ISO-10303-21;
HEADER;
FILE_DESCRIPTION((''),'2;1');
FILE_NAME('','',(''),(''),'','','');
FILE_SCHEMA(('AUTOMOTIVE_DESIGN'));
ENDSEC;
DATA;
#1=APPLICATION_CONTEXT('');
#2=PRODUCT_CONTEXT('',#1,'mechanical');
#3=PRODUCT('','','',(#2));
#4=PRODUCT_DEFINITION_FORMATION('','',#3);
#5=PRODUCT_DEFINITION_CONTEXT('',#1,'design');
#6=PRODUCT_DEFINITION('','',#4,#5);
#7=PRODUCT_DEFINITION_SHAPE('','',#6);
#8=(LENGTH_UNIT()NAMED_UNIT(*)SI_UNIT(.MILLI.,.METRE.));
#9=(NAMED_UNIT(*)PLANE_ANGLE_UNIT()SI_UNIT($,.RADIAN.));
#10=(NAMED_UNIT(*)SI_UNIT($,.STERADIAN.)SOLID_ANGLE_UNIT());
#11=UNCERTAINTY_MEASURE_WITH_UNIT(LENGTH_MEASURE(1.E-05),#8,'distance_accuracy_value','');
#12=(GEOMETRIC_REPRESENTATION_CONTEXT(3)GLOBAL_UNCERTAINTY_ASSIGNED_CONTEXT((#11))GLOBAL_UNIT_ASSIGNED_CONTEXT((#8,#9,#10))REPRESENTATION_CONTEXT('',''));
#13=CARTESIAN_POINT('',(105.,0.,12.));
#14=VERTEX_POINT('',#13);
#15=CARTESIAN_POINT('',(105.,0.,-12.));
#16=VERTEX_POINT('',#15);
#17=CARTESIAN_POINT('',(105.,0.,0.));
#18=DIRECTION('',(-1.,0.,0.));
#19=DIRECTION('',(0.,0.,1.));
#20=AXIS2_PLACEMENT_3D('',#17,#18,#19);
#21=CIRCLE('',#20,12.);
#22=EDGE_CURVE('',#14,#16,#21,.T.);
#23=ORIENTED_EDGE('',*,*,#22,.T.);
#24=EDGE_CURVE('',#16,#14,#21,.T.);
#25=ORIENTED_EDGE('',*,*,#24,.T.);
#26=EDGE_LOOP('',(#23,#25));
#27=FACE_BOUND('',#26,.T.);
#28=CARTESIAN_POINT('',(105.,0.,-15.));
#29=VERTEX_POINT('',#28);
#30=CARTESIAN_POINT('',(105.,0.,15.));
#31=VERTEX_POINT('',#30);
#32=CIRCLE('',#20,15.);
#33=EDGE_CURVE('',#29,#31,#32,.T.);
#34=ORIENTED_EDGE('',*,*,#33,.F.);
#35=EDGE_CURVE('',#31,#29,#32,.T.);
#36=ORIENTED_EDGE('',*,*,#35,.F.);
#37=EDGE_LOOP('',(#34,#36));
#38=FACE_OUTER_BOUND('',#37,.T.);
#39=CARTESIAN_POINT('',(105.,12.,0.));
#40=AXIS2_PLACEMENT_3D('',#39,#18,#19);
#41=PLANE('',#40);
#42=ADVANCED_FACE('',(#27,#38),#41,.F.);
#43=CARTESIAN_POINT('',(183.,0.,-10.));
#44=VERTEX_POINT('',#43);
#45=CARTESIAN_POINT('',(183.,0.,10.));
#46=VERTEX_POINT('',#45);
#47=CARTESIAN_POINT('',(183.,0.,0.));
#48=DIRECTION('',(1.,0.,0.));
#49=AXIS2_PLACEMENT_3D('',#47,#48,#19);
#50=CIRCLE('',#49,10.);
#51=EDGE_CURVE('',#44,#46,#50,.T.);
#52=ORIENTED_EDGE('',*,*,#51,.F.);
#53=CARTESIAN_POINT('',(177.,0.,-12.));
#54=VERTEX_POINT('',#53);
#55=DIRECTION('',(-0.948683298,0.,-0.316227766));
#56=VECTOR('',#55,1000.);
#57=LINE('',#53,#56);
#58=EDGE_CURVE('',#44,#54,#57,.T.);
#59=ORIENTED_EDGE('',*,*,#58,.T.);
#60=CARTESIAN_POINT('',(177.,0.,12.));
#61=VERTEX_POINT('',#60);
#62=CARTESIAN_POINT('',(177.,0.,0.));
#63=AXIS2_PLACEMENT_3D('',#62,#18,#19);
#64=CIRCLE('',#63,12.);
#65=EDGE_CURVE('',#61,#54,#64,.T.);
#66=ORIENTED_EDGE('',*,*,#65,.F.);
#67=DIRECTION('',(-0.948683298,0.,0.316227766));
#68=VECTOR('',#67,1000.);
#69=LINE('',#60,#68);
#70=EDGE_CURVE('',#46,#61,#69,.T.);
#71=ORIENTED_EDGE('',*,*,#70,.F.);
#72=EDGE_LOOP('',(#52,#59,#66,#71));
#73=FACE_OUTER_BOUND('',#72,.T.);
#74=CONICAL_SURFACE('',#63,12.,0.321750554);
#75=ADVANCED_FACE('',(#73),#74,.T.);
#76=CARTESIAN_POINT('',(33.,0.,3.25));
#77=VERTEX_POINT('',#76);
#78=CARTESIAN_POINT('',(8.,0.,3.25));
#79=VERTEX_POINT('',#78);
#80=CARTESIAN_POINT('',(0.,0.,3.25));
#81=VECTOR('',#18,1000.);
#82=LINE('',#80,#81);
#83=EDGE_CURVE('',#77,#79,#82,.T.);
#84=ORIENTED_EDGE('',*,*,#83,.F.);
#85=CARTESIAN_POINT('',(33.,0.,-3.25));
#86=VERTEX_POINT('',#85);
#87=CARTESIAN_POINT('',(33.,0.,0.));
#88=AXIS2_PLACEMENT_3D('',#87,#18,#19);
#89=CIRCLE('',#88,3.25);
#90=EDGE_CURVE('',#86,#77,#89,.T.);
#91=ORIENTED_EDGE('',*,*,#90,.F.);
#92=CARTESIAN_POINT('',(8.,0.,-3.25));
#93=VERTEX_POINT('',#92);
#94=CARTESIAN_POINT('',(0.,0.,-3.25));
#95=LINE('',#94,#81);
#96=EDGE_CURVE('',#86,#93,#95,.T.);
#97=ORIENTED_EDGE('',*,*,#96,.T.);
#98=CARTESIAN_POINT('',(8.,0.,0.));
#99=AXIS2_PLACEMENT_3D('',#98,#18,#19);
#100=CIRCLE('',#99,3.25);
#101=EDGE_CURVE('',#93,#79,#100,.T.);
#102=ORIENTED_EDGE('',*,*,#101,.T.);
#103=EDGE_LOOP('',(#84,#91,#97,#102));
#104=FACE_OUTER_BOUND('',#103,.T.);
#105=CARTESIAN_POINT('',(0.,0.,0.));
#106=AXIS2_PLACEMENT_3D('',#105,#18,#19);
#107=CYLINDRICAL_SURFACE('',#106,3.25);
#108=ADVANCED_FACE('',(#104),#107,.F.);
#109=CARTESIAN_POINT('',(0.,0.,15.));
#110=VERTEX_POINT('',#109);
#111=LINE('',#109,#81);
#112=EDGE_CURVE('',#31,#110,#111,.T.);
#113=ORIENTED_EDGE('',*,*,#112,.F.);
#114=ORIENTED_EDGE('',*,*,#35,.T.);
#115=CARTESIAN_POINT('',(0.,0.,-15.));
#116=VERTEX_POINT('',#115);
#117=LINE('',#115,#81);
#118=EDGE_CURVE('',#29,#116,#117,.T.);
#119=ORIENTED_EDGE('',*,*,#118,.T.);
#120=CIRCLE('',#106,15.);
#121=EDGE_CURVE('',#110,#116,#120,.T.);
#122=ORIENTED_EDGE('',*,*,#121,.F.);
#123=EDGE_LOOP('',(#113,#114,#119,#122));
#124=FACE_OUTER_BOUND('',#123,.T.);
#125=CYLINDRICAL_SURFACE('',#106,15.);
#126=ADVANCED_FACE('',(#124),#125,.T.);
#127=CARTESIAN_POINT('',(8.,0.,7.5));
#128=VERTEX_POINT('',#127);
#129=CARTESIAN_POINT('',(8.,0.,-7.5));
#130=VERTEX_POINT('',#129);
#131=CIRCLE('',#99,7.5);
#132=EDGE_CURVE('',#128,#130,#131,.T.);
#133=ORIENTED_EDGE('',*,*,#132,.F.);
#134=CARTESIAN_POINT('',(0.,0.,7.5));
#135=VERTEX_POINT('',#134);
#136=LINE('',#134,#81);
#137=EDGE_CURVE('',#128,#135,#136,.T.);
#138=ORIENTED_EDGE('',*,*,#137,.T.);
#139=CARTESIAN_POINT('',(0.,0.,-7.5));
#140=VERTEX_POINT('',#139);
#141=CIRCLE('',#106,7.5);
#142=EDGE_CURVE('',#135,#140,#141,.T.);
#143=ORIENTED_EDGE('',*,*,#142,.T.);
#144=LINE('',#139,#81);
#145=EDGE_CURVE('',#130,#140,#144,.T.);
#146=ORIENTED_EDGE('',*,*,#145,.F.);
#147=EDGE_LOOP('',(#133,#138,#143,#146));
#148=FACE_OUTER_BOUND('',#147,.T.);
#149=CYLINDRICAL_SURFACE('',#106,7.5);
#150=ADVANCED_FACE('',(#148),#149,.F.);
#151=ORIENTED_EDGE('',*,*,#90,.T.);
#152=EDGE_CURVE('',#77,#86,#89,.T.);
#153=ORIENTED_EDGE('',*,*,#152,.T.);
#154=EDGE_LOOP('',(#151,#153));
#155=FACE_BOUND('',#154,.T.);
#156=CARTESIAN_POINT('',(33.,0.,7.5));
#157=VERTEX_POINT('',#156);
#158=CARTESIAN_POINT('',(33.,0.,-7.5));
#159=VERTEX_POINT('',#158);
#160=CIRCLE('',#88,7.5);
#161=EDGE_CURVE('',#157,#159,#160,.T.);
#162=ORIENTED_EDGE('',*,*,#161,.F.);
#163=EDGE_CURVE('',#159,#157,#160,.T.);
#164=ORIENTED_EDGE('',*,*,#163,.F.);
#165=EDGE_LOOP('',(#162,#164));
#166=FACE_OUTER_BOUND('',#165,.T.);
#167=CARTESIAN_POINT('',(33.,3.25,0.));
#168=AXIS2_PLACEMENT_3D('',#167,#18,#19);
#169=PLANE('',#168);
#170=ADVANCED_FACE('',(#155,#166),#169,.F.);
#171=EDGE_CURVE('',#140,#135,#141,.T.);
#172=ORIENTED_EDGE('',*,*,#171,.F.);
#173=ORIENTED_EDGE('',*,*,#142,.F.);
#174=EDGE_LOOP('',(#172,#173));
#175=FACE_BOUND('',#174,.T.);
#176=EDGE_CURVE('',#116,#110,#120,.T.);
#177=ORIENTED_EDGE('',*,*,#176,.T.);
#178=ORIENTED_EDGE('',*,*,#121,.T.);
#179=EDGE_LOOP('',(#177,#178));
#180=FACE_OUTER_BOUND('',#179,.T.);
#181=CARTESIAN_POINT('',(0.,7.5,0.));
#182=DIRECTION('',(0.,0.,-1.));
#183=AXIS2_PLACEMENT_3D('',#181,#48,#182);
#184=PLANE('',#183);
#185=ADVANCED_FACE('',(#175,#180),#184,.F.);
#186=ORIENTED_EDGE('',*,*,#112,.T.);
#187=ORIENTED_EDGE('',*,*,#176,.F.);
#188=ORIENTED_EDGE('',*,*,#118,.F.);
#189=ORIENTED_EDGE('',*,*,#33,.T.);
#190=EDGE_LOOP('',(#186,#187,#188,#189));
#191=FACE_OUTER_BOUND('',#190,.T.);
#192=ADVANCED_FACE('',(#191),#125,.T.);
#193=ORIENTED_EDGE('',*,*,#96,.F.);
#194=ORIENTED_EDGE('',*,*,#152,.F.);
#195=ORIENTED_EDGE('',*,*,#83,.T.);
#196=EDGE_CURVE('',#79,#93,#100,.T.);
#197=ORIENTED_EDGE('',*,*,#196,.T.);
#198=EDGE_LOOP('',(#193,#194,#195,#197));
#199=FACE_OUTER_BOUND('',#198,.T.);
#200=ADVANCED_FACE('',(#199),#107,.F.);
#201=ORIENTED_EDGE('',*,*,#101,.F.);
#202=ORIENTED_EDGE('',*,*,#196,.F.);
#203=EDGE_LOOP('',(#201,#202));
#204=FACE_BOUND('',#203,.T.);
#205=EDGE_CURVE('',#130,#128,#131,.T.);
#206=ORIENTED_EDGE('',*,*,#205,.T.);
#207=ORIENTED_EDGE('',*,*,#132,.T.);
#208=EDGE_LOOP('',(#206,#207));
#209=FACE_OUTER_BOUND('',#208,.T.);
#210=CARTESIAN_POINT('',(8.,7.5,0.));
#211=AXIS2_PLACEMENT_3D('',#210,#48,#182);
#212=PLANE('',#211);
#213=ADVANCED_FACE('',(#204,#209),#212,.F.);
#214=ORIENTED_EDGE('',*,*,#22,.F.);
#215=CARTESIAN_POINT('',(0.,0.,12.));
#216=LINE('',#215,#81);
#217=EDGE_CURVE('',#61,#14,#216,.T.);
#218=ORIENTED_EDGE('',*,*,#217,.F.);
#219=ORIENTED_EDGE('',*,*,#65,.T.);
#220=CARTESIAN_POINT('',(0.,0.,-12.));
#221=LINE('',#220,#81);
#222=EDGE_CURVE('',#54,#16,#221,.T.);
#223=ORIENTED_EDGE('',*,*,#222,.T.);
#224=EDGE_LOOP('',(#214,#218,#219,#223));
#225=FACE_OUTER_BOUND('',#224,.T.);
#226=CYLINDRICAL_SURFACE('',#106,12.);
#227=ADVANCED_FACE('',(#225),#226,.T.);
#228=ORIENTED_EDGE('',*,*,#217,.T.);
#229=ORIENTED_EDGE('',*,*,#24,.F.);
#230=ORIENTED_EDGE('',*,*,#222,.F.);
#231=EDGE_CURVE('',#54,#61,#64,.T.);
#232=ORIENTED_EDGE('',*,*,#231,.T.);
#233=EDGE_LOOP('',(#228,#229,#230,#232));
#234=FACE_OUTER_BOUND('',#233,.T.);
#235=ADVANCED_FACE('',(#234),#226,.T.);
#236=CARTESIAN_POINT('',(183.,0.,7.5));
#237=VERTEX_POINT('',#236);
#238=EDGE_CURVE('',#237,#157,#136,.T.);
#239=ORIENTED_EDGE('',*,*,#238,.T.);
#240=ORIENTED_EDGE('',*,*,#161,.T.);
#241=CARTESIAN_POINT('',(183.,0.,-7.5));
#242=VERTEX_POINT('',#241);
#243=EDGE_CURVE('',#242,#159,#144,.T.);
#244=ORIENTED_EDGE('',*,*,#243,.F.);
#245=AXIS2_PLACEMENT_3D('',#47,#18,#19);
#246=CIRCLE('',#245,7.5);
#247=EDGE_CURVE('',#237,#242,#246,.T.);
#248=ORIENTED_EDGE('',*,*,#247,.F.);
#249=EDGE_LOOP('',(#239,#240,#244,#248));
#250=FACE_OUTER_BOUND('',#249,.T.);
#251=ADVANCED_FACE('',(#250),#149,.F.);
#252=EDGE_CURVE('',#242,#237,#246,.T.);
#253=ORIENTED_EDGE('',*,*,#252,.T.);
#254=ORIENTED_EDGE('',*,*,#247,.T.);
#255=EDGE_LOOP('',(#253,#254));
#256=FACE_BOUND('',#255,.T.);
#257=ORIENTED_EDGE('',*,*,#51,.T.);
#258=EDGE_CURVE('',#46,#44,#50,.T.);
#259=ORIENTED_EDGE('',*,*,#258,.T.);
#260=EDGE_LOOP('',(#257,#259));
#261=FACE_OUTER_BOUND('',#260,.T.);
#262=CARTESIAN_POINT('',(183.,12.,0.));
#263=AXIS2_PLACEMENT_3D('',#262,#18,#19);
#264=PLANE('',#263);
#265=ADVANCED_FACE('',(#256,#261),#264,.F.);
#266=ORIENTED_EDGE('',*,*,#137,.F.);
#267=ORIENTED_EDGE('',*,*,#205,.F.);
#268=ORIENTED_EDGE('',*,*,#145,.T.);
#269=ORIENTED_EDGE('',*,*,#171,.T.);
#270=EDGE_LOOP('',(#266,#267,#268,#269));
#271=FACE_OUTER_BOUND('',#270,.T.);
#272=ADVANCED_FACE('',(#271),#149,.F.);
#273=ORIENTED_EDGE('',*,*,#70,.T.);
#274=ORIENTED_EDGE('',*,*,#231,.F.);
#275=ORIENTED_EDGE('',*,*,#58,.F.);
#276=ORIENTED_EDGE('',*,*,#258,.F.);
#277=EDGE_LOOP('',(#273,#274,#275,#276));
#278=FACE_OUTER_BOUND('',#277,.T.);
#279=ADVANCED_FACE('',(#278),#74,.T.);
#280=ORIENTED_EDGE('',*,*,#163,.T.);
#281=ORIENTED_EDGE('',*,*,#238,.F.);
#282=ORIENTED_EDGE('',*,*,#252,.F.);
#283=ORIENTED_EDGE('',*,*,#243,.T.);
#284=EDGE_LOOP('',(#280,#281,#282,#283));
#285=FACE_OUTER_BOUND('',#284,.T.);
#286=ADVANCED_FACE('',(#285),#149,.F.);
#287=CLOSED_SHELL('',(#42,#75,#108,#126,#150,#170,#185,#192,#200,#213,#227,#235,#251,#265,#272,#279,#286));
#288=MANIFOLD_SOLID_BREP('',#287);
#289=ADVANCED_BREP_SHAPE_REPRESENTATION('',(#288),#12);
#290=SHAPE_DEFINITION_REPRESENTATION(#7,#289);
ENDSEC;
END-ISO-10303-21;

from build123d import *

# Parameters (mm, degrees)
CHAMFER1_SIZE  = 2
CHAMFER1_SIZE2 = 6


with BuildPart() as part:
    # Sketch1 → Revolve1 (revolve)
    with BuildSketch(Plane.XY, mode=Mode.PRIVATE) as revolve1_sk:
        Polygon((0, 7.5), (0, 15), (105, 15), (105, 12), (183, 12), (183, 7.5), (33, 7.5), (33, 3.25), (8, 3.25), (8, 7.5), align=None)
    revolve(revolve1_sk.sketch.rotate(Axis((0, 0, 0), (1, 0, 0)), 90), axis=Axis((0, 0, 0), (1, 0, 0)))

    # Chamfer1
    chamfer1_edges = [part.edges().sort_by_distance(p)[0] for p in [
        (183, 0, -12),
    ]]
    chamfer1_side = [part.faces().sort_by_distance(p)[0] for p in [
        (183, 0, -11.660588745),
    ]]
    chamfer(chamfer1_edges, length=CHAMFER1_SIZE, length2=CHAMFER1_SIZE2, reference=chamfer1_side[0])


solid = part.part
